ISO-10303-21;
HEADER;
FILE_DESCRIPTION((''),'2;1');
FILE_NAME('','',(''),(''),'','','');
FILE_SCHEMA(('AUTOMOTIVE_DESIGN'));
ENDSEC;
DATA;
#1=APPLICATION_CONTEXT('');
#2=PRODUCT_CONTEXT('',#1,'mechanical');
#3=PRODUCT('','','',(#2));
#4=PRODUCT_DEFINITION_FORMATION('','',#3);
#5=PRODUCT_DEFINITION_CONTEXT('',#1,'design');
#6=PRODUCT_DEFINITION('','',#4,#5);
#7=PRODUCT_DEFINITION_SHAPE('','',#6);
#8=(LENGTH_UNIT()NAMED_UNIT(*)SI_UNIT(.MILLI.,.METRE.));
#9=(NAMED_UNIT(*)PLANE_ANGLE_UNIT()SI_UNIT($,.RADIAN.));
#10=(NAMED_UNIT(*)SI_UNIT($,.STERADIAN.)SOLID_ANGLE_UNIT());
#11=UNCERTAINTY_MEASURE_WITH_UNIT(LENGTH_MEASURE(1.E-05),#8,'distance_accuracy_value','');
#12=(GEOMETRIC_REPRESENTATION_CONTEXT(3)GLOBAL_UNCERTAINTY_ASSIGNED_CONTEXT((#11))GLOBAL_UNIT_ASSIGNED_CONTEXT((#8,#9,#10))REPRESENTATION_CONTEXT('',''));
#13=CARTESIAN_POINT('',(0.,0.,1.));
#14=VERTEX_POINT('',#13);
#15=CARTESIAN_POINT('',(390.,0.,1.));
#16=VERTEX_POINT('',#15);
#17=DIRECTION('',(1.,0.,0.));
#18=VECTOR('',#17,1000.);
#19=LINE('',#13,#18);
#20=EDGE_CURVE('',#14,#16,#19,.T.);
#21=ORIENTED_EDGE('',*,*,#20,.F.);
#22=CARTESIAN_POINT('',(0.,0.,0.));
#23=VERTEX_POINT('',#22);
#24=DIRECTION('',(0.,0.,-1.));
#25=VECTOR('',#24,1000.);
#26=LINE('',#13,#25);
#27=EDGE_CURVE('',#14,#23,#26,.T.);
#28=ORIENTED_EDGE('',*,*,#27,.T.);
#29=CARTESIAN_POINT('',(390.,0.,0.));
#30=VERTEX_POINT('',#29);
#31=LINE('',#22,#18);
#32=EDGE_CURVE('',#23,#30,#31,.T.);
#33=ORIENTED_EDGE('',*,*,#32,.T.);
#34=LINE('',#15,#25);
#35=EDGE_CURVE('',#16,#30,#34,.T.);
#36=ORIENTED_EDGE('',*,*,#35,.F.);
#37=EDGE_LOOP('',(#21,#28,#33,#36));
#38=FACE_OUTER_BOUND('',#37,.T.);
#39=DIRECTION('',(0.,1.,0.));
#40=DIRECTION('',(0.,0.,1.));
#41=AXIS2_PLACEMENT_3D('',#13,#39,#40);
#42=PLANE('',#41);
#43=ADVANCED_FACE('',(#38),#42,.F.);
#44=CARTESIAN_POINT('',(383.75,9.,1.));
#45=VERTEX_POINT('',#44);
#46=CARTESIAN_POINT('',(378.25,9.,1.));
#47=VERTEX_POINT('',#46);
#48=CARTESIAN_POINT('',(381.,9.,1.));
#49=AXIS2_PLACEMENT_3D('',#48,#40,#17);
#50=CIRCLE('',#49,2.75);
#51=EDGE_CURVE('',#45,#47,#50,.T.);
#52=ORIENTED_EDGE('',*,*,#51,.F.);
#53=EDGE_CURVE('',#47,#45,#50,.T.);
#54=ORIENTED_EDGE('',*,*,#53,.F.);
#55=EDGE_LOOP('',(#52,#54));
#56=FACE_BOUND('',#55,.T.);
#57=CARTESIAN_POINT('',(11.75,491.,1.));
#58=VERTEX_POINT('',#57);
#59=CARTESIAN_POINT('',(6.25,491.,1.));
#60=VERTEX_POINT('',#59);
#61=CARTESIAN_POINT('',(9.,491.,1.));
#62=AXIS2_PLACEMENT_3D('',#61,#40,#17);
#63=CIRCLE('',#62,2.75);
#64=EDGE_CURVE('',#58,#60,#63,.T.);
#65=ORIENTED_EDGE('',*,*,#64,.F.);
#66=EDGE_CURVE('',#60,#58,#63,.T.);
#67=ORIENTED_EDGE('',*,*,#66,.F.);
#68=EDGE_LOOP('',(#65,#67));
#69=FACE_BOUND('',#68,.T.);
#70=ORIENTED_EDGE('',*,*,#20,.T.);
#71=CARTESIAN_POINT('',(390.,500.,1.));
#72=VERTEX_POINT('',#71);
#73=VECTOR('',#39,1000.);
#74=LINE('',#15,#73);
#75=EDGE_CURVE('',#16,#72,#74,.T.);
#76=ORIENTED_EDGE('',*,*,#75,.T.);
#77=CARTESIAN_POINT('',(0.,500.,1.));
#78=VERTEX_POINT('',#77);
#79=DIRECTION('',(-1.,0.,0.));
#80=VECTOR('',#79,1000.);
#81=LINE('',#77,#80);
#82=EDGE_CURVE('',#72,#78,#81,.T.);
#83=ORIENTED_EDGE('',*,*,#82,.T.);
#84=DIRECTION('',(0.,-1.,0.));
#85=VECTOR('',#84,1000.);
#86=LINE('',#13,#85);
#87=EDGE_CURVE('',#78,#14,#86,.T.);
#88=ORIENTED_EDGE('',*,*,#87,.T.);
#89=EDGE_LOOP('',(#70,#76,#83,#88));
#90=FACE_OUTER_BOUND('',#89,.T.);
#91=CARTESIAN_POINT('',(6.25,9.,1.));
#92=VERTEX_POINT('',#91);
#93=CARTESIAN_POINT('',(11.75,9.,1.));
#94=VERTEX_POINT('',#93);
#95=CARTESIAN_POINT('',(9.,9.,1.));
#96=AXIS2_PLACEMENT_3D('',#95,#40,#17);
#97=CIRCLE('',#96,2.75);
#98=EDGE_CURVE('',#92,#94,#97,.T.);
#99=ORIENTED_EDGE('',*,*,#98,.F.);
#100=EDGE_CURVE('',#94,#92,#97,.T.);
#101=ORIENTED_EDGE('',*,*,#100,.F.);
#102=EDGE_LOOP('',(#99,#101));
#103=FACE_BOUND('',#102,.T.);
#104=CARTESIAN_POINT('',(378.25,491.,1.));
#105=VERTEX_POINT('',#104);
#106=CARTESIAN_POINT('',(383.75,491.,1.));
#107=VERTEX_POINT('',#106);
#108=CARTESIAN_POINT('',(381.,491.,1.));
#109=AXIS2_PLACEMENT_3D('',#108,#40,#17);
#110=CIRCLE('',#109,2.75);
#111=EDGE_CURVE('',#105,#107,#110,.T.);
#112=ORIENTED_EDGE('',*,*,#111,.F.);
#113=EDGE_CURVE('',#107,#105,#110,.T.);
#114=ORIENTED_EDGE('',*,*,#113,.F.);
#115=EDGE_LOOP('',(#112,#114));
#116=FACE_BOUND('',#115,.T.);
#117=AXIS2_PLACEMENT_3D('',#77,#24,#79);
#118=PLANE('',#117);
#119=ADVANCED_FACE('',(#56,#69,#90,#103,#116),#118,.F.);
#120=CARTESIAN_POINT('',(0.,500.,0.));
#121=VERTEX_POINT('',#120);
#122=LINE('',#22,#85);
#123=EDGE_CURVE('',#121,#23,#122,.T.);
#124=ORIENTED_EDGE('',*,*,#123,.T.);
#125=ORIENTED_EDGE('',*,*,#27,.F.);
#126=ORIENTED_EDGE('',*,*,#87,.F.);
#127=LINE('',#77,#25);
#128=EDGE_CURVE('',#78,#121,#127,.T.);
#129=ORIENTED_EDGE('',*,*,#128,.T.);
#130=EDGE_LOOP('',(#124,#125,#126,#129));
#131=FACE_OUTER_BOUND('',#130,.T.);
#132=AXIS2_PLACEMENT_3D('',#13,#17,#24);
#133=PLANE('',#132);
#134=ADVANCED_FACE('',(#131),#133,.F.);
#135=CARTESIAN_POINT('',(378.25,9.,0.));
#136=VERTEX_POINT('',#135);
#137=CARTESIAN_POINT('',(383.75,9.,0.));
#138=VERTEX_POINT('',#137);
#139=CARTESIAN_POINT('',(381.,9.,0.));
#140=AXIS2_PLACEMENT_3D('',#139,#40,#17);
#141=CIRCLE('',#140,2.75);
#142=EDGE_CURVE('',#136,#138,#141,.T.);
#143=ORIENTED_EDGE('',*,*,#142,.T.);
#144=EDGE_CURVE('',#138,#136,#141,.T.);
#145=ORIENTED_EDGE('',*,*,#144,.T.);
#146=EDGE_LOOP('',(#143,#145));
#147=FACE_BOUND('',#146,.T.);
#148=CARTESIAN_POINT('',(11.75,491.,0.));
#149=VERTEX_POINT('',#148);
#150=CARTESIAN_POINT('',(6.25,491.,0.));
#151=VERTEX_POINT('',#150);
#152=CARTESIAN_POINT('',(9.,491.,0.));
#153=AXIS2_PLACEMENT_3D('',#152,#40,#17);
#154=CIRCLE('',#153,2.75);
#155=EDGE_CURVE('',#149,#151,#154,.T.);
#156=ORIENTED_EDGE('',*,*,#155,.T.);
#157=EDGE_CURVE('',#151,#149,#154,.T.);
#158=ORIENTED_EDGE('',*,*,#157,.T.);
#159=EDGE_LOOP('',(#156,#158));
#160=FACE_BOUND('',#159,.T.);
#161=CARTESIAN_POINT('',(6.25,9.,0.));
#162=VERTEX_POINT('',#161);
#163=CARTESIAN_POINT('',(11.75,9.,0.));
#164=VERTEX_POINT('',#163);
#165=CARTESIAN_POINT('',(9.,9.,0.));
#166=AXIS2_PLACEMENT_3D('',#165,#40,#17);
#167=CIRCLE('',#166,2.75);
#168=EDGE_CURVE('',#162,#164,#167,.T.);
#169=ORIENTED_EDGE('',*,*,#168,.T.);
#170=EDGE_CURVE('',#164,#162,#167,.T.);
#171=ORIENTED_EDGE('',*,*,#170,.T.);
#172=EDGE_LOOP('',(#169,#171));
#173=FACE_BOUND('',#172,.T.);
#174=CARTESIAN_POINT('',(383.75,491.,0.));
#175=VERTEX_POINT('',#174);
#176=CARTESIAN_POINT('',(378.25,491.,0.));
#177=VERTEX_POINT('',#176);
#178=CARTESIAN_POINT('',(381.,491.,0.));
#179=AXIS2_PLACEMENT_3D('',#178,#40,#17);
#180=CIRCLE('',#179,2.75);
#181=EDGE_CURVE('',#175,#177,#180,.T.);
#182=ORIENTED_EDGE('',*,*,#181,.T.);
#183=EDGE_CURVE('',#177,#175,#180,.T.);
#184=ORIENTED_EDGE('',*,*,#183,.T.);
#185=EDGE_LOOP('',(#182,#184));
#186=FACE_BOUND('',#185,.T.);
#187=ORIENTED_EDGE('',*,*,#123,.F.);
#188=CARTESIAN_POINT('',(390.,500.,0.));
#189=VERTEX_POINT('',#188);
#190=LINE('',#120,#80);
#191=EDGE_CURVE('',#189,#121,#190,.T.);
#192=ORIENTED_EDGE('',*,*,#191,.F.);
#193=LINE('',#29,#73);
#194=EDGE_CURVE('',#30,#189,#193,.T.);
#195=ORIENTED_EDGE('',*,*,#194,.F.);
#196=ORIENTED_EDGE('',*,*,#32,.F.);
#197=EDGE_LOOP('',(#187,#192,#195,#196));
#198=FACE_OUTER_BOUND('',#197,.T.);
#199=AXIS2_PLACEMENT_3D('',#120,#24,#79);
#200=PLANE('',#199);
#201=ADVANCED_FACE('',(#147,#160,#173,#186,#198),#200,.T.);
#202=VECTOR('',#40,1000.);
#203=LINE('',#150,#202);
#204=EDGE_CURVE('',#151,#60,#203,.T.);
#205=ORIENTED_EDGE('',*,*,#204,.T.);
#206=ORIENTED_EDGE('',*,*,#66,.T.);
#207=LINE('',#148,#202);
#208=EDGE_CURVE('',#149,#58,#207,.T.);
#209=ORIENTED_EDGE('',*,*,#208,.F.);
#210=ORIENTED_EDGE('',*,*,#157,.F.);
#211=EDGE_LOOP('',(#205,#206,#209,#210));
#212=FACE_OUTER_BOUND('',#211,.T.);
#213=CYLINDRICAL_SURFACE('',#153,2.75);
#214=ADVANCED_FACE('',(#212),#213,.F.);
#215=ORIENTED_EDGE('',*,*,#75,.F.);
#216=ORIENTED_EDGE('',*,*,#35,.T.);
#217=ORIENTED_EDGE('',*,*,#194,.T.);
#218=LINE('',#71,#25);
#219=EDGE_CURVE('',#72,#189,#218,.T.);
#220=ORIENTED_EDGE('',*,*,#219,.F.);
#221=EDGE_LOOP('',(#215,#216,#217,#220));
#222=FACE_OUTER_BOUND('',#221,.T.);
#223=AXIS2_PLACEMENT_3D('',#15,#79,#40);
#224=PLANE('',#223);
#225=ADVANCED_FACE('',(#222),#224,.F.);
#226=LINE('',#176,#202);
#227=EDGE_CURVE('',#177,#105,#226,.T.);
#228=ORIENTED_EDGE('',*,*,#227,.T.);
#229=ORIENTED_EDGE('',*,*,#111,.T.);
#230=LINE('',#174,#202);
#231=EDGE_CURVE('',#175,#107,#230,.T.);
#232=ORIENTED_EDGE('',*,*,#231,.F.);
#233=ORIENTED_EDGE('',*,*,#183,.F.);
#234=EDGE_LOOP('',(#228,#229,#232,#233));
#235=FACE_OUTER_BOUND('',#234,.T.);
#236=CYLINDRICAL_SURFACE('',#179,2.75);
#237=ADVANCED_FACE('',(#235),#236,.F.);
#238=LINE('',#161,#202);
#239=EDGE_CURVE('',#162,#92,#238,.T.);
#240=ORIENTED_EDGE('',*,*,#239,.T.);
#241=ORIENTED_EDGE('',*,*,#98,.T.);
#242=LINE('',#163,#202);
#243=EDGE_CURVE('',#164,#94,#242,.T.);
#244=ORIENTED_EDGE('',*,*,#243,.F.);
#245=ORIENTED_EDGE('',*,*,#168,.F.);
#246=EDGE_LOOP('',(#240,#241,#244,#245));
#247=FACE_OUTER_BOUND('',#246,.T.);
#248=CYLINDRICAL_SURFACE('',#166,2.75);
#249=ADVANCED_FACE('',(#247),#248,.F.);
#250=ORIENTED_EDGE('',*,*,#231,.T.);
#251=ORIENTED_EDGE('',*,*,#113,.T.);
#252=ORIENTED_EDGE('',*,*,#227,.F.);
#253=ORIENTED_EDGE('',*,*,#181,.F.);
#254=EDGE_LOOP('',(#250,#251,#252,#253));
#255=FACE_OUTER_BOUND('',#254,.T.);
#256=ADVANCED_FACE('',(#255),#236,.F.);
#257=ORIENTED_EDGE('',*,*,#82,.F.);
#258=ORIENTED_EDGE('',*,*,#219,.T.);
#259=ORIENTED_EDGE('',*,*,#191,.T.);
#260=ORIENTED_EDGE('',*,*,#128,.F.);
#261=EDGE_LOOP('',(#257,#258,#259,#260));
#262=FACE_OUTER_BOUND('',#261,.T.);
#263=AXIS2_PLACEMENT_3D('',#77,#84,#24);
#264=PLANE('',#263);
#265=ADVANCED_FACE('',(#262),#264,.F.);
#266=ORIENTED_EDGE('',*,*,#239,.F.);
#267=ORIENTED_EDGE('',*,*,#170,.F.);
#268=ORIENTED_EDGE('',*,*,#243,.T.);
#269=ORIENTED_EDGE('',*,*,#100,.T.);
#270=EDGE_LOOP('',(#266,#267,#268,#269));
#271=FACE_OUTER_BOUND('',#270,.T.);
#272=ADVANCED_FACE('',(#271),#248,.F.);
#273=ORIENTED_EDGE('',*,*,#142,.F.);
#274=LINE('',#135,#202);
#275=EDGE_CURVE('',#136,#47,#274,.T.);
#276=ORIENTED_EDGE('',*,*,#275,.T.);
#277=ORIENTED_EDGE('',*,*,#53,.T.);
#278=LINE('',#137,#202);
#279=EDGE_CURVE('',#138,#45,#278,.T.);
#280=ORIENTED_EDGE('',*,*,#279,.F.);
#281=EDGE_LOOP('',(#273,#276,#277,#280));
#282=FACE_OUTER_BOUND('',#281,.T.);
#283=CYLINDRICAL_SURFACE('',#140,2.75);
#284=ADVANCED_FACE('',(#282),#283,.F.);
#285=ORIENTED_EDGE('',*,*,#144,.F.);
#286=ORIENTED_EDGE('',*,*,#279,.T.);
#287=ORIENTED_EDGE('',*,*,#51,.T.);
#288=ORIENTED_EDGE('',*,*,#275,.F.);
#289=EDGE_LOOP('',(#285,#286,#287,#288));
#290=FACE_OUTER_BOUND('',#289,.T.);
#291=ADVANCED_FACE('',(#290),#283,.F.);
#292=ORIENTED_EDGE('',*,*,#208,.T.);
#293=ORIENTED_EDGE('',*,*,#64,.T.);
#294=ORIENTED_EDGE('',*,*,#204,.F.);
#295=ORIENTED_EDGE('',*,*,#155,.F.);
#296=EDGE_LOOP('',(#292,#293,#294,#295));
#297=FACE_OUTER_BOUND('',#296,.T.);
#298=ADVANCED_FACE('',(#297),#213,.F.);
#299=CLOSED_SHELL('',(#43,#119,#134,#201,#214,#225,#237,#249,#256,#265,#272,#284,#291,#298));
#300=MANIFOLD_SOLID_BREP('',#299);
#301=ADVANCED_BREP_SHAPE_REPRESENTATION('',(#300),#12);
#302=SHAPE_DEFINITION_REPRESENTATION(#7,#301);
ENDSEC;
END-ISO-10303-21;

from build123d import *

# Parameters (mm, degrees)
SKETCH_1_W          = 390
SKETCH_1_H          = 500
EXTRUDE_1_DEPTH     = 1
SKETCH_2_R          = 2.75
CUT_EXTRUDE_1_DEPTH = 1


with BuildPart() as part:
    # 草图1 → 凸台-拉伸1 (new body)
    with BuildSketch(Plane.XY):
        with Locations((195, 250)):
            Rectangle(SKETCH_1_W, SKETCH_1_H)
    extrude(amount=EXTRUDE_1_DEPTH)

    # 草图2 → 切除-拉伸1 (cut)
    with BuildSketch(Plane.XY.offset(1)):
        with Locations((9, 491)):
            Circle(SKETCH_2_R)
        with Locations((381, 491)):
            Circle(SKETCH_2_R)
        with Locations((9, 9)):
            Circle(SKETCH_2_R)
        with Locations((381, 9)):
            Circle(SKETCH_2_R)
    extrude(amount=-CUT_EXTRUDE_1_DEPTH, mode=Mode.SUBTRACT)


solid = part.part
